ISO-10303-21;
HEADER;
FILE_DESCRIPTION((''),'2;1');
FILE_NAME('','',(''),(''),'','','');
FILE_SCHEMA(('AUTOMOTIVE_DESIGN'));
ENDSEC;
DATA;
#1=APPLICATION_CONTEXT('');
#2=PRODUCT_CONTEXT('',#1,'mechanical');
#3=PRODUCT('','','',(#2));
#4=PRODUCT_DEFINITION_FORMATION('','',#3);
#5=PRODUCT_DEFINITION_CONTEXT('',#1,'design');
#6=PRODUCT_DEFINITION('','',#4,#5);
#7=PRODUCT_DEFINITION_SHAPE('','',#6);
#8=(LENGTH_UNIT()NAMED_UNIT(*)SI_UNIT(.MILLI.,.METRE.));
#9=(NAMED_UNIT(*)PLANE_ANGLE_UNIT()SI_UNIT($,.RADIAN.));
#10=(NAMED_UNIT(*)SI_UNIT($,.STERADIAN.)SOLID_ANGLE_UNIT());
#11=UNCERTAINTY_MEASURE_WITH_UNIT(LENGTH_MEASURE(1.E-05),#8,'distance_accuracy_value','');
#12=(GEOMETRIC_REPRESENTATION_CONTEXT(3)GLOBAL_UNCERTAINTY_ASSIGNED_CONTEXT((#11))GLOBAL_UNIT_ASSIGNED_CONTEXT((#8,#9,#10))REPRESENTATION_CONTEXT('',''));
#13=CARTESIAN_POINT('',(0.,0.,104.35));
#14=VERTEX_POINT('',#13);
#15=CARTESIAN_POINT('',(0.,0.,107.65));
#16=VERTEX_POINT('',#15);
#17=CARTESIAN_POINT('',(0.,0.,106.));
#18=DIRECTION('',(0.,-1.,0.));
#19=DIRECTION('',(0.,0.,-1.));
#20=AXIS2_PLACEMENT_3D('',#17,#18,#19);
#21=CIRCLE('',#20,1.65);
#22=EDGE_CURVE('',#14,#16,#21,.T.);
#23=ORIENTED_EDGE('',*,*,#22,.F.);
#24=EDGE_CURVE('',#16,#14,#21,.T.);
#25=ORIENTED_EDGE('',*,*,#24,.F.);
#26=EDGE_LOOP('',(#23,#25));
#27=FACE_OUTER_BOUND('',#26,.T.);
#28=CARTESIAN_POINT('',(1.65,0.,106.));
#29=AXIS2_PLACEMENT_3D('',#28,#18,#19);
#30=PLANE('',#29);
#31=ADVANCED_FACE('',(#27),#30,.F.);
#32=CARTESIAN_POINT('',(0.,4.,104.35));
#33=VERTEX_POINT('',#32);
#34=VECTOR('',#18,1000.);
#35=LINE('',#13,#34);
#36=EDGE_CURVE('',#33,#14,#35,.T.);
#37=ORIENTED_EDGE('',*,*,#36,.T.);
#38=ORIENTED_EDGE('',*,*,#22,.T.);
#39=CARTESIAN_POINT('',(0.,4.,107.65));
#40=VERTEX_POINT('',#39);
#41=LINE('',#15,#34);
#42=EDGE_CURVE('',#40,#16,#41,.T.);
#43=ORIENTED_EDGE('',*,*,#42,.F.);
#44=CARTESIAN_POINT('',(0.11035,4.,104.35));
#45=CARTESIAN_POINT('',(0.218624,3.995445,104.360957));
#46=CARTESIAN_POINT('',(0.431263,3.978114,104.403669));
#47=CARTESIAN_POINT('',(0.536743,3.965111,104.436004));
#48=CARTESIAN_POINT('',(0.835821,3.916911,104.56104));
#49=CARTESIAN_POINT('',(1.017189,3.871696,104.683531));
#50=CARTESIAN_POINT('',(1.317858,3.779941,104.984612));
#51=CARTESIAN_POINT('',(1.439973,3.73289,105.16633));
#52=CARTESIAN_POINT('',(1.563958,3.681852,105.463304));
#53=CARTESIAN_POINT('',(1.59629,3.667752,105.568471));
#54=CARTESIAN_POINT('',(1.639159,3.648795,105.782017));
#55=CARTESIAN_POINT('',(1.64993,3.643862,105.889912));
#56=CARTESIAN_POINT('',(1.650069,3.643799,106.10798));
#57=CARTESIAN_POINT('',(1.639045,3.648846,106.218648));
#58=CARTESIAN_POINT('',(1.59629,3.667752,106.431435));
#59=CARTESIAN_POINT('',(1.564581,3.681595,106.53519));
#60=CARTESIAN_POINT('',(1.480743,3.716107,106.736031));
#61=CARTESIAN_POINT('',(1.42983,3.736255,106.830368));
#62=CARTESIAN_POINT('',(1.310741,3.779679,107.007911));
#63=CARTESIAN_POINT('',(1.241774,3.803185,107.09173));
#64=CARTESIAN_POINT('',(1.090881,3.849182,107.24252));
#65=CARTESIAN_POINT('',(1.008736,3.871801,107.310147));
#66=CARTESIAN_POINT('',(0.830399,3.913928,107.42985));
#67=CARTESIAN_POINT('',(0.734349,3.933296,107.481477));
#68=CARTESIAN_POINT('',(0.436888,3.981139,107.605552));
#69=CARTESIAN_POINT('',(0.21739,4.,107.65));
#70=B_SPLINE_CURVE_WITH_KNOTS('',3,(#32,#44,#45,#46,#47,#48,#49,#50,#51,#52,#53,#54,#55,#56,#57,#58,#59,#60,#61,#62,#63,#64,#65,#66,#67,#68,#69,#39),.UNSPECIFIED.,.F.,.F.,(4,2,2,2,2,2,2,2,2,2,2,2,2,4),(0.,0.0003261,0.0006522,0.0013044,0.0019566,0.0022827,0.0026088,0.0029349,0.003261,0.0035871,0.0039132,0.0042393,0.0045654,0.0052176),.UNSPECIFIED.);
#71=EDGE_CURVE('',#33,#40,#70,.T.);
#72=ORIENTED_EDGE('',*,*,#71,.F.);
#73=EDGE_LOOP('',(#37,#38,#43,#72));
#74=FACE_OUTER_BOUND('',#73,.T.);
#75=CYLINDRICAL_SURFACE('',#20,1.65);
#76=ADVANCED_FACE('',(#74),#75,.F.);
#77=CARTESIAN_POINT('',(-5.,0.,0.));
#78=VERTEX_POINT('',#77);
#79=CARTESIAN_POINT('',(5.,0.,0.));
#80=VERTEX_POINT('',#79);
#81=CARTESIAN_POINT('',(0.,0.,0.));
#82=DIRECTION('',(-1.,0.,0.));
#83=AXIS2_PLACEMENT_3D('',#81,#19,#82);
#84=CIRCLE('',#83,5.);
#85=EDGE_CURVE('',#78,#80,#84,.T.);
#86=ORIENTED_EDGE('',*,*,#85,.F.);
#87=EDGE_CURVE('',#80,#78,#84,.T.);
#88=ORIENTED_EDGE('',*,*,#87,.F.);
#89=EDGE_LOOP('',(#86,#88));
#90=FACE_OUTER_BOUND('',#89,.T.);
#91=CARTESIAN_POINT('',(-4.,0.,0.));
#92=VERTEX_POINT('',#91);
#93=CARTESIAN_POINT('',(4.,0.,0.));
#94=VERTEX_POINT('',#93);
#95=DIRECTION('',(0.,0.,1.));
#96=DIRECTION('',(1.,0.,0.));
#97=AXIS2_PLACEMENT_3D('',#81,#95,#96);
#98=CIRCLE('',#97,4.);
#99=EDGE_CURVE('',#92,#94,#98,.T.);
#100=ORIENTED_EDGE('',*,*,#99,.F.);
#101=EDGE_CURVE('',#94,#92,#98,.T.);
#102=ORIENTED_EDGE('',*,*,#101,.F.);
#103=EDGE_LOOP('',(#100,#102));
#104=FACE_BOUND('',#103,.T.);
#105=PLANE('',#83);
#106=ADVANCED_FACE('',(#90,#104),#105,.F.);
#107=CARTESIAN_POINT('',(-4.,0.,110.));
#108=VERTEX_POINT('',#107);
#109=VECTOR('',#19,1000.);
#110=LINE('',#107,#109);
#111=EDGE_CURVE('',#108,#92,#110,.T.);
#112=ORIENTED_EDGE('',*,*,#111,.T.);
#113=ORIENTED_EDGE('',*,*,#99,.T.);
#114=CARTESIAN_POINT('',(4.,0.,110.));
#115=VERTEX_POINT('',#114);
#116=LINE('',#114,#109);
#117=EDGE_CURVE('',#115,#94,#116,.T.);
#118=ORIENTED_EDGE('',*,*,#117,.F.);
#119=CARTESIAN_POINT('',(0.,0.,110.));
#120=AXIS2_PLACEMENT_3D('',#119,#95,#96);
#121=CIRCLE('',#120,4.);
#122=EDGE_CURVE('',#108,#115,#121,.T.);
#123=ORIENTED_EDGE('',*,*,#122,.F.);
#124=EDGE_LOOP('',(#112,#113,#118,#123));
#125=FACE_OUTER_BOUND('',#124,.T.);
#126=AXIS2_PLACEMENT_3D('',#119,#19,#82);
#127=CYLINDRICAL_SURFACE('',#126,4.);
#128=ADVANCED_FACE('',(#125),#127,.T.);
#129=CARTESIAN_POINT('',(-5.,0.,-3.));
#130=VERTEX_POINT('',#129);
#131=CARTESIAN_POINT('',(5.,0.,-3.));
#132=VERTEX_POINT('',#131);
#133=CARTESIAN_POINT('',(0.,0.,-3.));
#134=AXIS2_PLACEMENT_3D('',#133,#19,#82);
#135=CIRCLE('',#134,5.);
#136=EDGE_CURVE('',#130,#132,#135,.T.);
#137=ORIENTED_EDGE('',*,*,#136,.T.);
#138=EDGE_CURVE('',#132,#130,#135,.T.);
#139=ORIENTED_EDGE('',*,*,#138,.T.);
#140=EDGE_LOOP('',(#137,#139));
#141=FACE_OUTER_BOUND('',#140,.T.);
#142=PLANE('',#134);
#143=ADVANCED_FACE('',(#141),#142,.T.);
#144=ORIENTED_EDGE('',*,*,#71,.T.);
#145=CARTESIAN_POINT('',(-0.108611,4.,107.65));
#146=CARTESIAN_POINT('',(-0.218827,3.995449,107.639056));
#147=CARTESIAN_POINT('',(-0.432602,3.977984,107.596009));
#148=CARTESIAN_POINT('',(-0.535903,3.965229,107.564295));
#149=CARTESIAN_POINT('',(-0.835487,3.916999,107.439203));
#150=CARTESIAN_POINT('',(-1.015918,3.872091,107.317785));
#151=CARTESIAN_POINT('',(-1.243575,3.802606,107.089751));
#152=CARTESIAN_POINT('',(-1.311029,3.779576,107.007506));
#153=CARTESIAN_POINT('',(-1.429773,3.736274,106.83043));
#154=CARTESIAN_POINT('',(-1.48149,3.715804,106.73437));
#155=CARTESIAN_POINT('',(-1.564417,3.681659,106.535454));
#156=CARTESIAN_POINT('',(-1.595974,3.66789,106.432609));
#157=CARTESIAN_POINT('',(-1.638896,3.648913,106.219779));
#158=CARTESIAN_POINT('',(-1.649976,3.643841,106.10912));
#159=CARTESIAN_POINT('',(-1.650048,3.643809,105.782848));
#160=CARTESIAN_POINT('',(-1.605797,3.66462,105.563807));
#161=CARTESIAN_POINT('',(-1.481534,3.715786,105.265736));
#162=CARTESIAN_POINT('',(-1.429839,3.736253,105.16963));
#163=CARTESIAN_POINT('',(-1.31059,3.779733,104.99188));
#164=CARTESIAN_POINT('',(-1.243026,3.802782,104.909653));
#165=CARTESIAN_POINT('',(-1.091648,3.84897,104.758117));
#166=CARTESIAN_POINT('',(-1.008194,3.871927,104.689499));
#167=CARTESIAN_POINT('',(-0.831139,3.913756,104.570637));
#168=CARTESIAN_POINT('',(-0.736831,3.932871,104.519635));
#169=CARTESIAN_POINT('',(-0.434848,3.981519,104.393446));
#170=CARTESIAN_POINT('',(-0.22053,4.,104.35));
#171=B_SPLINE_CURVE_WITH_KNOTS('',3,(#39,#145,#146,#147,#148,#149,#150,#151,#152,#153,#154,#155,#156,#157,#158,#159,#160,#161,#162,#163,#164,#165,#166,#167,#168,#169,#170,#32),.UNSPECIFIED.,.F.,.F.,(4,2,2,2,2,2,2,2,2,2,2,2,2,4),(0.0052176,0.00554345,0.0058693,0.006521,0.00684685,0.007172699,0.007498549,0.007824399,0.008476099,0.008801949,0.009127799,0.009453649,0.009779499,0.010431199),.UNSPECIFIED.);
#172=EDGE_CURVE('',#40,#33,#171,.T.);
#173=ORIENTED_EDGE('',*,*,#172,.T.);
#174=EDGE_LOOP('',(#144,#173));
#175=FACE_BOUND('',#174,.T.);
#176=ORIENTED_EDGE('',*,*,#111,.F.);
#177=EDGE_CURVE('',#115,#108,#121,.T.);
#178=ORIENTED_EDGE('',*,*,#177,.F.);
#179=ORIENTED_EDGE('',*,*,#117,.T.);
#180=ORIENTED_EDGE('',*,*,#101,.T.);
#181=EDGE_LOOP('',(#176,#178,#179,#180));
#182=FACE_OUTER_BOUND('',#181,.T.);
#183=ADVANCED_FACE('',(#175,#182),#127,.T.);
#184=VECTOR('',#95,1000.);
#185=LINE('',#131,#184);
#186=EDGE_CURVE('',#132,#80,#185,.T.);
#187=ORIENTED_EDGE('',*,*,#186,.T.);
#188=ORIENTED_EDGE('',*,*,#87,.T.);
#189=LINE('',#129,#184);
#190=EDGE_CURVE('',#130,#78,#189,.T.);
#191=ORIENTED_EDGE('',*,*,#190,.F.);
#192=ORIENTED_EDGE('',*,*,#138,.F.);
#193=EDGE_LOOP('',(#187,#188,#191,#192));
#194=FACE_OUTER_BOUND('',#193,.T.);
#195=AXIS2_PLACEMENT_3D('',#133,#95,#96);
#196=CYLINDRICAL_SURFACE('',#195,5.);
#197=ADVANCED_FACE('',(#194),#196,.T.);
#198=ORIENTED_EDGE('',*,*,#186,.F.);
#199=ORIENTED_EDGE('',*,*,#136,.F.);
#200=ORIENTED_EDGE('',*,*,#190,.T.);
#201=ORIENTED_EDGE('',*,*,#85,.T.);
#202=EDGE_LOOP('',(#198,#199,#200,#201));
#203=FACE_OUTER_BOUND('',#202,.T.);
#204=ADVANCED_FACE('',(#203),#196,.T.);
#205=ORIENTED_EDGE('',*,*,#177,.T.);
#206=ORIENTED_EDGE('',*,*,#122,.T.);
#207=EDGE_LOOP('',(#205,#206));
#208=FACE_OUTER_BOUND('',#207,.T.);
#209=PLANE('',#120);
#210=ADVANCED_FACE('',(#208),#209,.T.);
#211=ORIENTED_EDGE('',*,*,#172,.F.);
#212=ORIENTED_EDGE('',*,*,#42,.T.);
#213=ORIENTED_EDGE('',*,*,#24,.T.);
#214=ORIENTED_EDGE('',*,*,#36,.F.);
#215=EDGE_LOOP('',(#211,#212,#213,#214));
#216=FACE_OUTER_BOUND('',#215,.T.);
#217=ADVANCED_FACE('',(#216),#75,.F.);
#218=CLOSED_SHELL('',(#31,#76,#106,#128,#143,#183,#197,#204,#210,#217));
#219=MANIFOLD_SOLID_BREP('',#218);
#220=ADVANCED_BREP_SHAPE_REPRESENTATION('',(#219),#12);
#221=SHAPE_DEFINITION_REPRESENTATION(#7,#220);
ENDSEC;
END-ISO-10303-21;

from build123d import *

# Parameters (mm, degrees)
SKETCH1_R           = 4
BOSS_EXTRUDE1_DEPTH = 110
SKETCH7_R           = 5
BOSS_EXTRUDE2_DEPTH = 3
SKETCH9_W           = 1.65
SKETCH9_H           = 5


with BuildPart() as part:
    # Sketch1 → Boss-Extrude1 (new body)
    with BuildSketch(Plane.XY):
        Circle(SKETCH1_R)
    extrude(amount=BOSS_EXTRUDE1_DEPTH)

    # Sketch7 → Boss-Extrude2 (add)
    with BuildSketch(Plane(origin=(0, 0, 0), x_dir=(-1, 0, 0), z_dir=(0, 0, -1))):
        Circle(SKETCH7_R)
    extrude(amount=BOSS_EXTRUDE2_DEPTH)

    # Sketch9 → M4 Tapped Hole1 (revolve, cut)
    with BuildSketch(Plane(origin=(0, 0, 106), x_dir=(0, 0, -1), z_dir=(1, 0, 0))):
        with Locations((0.825, 2.5)):
            Rectangle(SKETCH9_W, SKETCH9_H)
    revolve(axis=Axis((0, -6.35, 106), (0, 1, 0)), mode=Mode.SUBTRACT)


solid = part.part
